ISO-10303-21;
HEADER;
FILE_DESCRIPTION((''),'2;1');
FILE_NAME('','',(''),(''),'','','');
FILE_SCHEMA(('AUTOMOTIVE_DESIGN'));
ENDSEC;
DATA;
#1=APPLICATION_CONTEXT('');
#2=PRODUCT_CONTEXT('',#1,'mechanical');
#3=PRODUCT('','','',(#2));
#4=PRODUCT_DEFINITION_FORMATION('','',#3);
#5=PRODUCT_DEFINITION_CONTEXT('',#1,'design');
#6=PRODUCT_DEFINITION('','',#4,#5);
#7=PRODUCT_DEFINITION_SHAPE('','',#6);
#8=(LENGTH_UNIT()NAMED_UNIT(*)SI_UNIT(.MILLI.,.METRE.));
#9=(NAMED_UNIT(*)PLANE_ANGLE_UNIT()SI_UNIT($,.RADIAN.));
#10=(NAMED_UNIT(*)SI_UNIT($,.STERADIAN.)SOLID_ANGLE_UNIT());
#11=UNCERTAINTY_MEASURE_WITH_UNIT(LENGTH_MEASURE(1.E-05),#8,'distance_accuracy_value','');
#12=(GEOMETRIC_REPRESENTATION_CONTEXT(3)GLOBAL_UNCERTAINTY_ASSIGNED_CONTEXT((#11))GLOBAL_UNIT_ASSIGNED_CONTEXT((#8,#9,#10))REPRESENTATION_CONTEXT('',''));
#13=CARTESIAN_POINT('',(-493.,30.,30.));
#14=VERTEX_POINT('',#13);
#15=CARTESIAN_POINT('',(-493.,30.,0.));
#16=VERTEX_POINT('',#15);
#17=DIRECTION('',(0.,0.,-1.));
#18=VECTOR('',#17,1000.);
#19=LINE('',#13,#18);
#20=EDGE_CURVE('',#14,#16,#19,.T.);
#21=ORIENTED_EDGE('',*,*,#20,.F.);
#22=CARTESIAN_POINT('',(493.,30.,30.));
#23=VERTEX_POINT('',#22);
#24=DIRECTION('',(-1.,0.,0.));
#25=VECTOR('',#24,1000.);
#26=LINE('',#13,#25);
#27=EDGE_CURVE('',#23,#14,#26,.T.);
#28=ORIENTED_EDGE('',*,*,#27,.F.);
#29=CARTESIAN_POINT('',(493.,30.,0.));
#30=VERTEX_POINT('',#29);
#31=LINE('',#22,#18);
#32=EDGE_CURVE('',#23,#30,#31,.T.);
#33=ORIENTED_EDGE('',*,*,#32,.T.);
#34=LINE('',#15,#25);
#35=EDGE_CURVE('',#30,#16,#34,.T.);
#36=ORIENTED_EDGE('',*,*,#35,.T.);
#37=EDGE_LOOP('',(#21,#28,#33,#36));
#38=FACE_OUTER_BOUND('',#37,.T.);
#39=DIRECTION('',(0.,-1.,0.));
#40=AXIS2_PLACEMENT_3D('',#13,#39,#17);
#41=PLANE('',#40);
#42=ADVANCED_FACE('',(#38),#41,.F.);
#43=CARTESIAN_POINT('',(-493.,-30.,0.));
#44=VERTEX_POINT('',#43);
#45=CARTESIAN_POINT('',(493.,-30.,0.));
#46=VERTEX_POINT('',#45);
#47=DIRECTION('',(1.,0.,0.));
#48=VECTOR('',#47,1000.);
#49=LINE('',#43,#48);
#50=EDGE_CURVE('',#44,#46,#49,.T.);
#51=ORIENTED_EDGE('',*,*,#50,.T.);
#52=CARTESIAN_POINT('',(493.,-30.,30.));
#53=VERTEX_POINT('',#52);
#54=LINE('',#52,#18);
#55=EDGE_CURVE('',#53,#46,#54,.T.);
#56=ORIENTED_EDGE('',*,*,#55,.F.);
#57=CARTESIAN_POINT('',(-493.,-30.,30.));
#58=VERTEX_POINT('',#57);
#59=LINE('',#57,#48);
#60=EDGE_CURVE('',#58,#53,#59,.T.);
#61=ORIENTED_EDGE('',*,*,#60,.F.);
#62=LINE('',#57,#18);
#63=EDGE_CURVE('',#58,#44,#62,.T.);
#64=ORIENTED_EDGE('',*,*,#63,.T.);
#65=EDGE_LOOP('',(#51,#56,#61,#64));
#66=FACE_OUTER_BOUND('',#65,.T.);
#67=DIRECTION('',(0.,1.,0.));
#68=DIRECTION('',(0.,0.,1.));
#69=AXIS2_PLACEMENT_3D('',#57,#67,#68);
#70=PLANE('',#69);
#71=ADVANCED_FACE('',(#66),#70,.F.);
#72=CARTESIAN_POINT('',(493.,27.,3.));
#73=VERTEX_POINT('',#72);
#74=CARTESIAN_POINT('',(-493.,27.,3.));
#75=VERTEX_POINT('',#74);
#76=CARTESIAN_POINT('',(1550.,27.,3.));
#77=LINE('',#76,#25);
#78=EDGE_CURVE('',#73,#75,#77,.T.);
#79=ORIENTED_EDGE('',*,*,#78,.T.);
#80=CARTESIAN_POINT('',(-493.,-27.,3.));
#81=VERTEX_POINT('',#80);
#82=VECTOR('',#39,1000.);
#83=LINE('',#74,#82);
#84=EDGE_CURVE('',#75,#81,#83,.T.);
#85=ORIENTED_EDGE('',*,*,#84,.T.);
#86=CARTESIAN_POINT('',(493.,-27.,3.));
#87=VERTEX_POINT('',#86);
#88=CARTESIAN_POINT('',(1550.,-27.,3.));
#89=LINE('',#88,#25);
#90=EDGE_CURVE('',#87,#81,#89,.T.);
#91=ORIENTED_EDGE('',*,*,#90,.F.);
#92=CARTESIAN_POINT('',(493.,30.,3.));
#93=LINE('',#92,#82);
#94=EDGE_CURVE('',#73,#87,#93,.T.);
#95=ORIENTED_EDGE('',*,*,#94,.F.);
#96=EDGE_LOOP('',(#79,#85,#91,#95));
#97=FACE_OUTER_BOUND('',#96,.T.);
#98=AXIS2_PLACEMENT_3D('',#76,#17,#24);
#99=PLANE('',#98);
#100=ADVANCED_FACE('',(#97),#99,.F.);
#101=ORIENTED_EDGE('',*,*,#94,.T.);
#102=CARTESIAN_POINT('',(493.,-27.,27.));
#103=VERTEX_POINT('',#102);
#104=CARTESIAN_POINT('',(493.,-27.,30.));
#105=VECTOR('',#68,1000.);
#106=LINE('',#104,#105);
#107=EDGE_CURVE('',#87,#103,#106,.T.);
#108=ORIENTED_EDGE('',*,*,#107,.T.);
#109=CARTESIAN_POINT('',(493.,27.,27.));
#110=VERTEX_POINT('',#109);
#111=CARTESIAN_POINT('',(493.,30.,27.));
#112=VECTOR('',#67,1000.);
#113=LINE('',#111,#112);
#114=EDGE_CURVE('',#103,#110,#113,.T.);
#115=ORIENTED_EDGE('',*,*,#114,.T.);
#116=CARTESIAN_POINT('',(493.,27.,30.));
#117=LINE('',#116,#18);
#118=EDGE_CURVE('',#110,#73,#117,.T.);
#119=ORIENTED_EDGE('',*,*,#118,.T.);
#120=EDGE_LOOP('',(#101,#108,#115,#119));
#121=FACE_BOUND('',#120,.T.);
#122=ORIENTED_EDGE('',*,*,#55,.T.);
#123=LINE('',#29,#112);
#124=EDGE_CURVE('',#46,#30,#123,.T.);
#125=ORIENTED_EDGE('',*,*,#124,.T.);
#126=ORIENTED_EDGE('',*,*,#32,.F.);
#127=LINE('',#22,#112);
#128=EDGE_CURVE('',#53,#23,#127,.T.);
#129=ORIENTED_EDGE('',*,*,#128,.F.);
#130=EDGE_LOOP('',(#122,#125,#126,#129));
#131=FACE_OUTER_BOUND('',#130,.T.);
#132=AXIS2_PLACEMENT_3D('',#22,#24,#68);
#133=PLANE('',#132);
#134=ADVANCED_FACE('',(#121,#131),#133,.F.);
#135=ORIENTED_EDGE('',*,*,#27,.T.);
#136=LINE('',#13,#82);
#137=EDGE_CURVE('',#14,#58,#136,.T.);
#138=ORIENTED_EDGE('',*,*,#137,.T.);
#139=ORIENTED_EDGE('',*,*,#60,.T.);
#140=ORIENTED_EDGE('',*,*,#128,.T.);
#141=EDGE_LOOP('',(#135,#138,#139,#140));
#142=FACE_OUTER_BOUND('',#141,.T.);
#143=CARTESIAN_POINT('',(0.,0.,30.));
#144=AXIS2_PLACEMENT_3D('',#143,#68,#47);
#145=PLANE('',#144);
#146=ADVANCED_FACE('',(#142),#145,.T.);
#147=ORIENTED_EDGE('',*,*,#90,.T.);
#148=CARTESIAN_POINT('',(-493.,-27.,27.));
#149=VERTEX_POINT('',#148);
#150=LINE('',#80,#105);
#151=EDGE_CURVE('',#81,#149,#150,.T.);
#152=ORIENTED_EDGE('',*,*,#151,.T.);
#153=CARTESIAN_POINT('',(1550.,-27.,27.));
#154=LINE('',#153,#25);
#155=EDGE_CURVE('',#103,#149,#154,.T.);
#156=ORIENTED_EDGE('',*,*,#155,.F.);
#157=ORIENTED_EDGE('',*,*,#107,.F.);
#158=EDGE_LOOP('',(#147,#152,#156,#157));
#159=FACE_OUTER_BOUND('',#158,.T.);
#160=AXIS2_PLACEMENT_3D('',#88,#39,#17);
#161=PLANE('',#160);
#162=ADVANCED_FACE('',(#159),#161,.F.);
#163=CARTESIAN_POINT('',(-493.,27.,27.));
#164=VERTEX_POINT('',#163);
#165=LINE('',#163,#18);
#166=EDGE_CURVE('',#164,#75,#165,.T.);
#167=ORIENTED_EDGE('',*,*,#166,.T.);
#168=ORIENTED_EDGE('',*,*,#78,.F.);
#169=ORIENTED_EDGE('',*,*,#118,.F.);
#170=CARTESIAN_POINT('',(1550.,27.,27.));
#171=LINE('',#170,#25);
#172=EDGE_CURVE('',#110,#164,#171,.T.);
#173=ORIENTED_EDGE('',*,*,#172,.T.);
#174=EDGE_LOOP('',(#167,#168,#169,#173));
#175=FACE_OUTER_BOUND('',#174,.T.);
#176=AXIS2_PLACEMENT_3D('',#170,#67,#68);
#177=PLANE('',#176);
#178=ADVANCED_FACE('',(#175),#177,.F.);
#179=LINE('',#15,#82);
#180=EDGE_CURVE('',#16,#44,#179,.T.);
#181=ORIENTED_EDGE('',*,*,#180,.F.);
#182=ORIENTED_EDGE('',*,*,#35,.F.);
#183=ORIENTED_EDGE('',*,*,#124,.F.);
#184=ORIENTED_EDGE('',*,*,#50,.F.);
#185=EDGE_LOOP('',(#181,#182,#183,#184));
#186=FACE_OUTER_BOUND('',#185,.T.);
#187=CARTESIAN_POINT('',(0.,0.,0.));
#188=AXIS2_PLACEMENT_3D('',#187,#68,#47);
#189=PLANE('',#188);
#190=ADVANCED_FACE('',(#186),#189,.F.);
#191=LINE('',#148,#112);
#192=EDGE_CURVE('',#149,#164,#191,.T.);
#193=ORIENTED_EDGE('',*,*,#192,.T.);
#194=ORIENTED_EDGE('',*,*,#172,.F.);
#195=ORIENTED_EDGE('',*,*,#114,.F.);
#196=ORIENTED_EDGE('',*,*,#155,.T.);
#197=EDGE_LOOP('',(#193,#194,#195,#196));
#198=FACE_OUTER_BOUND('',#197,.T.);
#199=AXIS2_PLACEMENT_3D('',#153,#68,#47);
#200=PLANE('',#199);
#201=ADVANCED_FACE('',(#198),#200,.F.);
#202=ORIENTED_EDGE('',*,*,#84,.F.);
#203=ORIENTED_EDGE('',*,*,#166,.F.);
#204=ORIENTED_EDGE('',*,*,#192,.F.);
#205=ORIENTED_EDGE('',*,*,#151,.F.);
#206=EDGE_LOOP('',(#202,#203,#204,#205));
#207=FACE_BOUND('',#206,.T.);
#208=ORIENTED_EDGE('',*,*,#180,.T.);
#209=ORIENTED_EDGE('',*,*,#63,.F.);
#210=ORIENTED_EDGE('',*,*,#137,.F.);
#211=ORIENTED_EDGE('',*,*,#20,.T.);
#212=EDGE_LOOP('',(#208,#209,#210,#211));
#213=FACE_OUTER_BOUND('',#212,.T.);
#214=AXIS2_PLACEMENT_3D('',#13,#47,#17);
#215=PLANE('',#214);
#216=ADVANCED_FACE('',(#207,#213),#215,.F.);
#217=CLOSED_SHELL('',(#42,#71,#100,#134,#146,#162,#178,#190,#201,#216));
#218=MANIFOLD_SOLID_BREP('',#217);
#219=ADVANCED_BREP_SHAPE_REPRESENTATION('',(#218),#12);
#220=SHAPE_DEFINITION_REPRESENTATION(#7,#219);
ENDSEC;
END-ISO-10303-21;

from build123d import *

# Parameters (mm, degrees)
SKETCH1_W           = 986
SKETCH1_H           = 60
BOSS_EXTRUDE1_DEPTH = 30
SKETCH2_W           = 24
SKETCH2_H           = 54
CUT_EXTRUDE1_DEPTH  = 2043


with BuildPart() as part:
    # Sketch1 → Boss-Extrude1 (new body)
    with BuildSketch(Plane.XY):
        Rectangle(SKETCH1_W, SKETCH1_H)
    extrude(amount=BOSS_EXTRUDE1_DEPTH)

    # Sketch2 → Cut-Extrude1 (cut)
    with BuildSketch(Plane.ZY.offset(493)):
        with Locations((15, 0)):
            Rectangle(SKETCH2_W, SKETCH2_H)
    extrude(amount=-CUT_EXTRUDE1_DEPTH, mode=Mode.SUBTRACT)


solid = part.part
